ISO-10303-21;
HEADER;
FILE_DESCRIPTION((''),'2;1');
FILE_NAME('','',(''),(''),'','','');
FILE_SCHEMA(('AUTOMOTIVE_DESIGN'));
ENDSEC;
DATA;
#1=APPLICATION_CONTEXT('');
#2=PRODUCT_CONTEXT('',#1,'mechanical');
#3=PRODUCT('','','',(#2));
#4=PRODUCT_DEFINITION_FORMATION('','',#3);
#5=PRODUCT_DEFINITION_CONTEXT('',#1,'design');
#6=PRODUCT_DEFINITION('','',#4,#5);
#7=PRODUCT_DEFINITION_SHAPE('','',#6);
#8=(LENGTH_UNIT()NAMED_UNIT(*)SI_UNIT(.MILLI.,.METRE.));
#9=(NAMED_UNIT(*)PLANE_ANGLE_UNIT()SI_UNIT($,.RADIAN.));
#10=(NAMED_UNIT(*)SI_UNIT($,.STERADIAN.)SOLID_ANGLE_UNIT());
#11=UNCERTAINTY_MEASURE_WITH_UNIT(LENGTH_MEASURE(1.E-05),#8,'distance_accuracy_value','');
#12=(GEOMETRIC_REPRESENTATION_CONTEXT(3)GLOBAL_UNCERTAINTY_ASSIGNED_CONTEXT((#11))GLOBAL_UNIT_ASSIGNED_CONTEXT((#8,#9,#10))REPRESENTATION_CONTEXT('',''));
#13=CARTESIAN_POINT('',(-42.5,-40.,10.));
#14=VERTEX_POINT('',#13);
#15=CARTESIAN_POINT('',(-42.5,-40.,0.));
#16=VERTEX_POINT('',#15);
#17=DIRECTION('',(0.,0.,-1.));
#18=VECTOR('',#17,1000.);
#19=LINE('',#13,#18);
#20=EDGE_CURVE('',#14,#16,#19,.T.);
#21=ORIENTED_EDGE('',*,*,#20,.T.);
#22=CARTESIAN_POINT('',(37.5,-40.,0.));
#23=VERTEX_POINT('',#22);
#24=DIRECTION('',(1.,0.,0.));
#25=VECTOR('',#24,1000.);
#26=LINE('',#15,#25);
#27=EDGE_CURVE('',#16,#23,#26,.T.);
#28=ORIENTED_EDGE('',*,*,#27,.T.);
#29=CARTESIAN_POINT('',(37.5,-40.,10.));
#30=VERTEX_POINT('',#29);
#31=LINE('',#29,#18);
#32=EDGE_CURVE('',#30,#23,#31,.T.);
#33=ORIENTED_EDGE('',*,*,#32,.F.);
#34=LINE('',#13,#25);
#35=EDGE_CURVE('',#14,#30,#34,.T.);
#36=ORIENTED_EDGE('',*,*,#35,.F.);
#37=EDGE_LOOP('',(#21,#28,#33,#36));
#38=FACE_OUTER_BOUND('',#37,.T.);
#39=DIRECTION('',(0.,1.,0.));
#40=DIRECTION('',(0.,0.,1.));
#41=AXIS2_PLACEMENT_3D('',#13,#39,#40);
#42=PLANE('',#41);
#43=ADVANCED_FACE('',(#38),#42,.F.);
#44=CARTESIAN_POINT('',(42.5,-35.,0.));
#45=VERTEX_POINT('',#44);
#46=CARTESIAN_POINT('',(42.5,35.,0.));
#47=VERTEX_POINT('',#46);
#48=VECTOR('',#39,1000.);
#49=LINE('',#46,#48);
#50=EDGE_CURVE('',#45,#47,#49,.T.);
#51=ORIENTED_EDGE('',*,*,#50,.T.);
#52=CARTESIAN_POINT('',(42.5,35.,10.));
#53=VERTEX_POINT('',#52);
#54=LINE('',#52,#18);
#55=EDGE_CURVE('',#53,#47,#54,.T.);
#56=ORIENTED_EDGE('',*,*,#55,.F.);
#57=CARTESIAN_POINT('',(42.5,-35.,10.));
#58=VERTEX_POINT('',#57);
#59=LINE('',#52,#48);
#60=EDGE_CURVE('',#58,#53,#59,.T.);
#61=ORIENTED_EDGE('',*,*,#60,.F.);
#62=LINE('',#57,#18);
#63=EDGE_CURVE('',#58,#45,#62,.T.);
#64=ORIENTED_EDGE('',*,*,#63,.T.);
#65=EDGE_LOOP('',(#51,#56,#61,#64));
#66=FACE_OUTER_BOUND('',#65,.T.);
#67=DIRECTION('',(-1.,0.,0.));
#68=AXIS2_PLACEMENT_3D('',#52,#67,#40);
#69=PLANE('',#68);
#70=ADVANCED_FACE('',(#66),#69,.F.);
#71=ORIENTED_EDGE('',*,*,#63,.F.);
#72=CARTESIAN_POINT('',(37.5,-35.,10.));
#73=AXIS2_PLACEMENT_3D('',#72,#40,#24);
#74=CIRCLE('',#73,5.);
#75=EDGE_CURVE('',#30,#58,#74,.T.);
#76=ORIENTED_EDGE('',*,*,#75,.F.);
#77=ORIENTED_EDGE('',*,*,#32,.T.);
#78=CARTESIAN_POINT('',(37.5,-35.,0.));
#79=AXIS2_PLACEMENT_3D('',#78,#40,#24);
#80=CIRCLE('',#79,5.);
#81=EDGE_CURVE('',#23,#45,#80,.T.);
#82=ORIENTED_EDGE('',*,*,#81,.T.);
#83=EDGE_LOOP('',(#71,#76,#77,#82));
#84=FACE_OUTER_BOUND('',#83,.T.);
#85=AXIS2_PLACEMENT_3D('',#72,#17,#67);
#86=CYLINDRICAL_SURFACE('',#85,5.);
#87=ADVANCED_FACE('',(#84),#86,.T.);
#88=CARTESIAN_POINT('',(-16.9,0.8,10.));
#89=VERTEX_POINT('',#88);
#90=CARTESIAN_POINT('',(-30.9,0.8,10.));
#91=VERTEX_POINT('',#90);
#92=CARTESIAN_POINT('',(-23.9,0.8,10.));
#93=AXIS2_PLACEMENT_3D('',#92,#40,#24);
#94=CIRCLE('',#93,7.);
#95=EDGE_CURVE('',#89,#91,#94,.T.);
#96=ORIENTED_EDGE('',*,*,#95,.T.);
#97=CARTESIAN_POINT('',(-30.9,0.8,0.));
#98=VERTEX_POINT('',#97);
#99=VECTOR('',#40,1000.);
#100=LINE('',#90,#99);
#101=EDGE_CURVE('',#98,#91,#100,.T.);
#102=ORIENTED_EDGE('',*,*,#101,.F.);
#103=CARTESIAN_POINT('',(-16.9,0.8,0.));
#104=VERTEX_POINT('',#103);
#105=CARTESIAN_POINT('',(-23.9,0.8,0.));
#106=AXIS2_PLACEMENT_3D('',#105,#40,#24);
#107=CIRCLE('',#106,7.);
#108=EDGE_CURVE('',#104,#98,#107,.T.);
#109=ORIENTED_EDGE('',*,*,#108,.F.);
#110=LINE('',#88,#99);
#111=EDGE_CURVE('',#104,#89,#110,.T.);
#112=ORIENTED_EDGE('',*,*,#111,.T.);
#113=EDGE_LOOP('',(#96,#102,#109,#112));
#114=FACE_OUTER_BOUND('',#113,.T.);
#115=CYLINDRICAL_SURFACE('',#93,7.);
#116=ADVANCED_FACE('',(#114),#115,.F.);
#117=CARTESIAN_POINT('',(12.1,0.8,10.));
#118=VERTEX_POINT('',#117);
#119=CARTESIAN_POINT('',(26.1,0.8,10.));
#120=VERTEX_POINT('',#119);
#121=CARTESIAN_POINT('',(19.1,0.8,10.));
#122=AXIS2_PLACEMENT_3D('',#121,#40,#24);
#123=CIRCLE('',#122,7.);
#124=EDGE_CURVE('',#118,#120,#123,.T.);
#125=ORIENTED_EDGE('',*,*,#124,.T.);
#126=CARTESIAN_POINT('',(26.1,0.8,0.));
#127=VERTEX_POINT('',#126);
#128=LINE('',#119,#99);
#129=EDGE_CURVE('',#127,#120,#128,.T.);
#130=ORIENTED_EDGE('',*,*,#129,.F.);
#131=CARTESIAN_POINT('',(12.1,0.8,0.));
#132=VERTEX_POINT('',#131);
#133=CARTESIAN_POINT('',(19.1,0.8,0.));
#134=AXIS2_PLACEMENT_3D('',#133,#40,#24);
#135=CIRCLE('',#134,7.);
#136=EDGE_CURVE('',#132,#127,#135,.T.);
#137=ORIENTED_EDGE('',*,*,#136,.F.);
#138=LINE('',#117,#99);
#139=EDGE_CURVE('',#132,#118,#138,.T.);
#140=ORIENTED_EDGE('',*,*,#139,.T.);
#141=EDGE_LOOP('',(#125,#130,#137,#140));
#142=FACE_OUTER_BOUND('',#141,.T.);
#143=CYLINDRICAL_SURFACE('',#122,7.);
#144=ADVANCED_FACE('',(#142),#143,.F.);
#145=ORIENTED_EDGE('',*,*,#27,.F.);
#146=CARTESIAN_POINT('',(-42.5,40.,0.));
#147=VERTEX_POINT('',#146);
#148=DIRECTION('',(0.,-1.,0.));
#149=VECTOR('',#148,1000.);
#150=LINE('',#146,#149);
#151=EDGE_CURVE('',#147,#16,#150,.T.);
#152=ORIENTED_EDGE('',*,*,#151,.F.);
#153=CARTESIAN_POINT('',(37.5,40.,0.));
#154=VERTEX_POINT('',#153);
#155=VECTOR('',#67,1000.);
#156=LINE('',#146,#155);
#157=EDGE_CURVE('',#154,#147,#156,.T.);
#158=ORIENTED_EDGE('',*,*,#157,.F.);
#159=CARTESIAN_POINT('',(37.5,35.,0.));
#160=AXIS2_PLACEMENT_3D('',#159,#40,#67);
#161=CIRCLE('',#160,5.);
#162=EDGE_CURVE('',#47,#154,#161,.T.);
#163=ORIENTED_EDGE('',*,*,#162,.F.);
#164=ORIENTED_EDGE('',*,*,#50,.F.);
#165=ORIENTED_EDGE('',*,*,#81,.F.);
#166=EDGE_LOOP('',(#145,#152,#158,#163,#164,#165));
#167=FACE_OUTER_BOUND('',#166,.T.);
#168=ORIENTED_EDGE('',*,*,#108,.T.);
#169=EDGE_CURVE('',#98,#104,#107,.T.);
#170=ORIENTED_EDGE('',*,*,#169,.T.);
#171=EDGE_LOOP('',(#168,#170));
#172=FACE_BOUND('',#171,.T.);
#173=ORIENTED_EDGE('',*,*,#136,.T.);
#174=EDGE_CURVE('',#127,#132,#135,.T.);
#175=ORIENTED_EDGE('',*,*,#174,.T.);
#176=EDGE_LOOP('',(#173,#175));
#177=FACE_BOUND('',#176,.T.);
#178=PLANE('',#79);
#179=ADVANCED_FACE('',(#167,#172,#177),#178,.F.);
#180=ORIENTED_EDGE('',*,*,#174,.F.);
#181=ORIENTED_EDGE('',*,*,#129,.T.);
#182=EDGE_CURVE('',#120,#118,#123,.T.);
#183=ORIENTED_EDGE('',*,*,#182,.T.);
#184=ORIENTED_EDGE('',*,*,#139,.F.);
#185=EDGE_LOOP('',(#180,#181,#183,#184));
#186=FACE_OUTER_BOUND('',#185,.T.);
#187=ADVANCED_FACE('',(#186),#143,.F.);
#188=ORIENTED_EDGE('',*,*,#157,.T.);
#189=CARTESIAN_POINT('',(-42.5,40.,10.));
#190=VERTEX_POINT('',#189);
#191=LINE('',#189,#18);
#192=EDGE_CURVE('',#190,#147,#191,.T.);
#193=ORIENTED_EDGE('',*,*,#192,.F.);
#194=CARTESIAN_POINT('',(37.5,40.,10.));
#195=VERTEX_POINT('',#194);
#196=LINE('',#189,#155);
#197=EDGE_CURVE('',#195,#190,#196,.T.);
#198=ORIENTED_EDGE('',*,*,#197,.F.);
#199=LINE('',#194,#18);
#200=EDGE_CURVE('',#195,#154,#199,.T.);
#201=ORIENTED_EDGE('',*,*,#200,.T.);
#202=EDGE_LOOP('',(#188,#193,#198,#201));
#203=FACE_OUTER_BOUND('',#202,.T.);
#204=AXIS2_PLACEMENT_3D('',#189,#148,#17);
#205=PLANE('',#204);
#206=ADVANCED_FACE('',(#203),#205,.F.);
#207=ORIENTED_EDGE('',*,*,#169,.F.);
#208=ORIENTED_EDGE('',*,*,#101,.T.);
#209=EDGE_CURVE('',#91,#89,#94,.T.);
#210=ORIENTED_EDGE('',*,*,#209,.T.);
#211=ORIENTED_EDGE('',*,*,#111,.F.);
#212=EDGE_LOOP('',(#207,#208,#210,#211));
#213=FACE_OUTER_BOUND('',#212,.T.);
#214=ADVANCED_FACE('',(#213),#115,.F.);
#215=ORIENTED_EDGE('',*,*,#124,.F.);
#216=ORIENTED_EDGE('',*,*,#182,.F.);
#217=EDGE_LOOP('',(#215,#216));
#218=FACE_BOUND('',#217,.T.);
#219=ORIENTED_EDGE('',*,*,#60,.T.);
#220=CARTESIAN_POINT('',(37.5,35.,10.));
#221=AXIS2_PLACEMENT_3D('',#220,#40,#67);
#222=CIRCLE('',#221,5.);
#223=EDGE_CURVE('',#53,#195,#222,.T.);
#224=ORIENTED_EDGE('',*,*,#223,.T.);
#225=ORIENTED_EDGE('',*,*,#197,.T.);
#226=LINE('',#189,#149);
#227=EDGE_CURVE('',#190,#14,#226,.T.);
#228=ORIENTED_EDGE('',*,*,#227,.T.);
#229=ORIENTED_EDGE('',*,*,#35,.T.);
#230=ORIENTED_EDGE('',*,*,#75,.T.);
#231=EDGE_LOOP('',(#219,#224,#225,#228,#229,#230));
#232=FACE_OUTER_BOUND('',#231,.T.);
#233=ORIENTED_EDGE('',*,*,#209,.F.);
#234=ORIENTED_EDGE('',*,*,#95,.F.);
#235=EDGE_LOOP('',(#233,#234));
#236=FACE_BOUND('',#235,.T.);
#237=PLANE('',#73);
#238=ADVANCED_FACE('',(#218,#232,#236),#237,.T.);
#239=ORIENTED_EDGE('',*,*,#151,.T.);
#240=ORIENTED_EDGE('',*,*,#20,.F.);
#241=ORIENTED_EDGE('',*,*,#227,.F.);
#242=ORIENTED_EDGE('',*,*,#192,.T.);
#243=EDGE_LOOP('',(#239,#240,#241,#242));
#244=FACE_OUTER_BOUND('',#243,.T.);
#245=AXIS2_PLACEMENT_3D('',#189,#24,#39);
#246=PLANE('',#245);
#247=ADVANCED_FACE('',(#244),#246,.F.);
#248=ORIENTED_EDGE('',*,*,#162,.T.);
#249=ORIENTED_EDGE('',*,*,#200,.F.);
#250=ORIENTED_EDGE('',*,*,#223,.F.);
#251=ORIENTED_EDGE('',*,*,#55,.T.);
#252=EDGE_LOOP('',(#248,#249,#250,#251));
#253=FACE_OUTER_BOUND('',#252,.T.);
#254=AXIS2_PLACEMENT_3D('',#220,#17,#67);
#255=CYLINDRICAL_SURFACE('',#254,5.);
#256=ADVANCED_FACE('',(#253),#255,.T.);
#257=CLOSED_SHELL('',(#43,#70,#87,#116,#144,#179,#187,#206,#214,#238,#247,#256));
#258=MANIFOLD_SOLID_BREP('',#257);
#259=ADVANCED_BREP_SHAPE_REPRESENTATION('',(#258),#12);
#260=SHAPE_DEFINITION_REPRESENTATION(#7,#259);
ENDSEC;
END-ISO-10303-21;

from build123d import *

# Parameters (mm, degrees)
EXTRUDE_1_DEPTH             = 10
HOLE_WIZARD_14_0_14_1_D     = 14
HOLE_WIZARD_14_0_14_1_DEPTH = 19.793975667
HOLE_WIZARD_14_0_14_1_TIP   = 4.206024333


with BuildPart() as part:
    # 草图1 → 凸台-拉伸1 (new body)
    with BuildSketch(Plane.XY):
        with BuildLine():
            Line((-42.5, 40), (37.5, 40))
            ThreePointArc((37.5, 40), (41.035533906, 38.535533906), (42.5, 35))
            Line((42.5, 35), (42.5, -35))
            ThreePointArc((42.5, -35), (41.035533906, -38.535533906), (37.5, -40))
            Line((37.5, -40), (-42.5, -40))
            Line((-42.5, -40), (-42.5, 40))
        make_face()
    extrude(amount=EXTRUDE_1_DEPTH)

    # Ø14.0 (14) 直径孔1
    with Locations(Plane.XY.offset(10)):
        with Locations((19.1, 0.8), (-23.9, 0.8)):
            Hole(HOLE_WIZARD_14_0_14_1_D / 2, depth=HOLE_WIZARD_14_0_14_1_DEPTH)
            with Locations((0, 0, -(HOLE_WIZARD_14_0_14_1_DEPTH + HOLE_WIZARD_14_0_14_1_TIP / 2))):  # 118° drill point
                Cone(0, HOLE_WIZARD_14_0_14_1_D / 2, HOLE_WIZARD_14_0_14_1_TIP, mode=Mode.SUBTRACT)


solid = part.part
